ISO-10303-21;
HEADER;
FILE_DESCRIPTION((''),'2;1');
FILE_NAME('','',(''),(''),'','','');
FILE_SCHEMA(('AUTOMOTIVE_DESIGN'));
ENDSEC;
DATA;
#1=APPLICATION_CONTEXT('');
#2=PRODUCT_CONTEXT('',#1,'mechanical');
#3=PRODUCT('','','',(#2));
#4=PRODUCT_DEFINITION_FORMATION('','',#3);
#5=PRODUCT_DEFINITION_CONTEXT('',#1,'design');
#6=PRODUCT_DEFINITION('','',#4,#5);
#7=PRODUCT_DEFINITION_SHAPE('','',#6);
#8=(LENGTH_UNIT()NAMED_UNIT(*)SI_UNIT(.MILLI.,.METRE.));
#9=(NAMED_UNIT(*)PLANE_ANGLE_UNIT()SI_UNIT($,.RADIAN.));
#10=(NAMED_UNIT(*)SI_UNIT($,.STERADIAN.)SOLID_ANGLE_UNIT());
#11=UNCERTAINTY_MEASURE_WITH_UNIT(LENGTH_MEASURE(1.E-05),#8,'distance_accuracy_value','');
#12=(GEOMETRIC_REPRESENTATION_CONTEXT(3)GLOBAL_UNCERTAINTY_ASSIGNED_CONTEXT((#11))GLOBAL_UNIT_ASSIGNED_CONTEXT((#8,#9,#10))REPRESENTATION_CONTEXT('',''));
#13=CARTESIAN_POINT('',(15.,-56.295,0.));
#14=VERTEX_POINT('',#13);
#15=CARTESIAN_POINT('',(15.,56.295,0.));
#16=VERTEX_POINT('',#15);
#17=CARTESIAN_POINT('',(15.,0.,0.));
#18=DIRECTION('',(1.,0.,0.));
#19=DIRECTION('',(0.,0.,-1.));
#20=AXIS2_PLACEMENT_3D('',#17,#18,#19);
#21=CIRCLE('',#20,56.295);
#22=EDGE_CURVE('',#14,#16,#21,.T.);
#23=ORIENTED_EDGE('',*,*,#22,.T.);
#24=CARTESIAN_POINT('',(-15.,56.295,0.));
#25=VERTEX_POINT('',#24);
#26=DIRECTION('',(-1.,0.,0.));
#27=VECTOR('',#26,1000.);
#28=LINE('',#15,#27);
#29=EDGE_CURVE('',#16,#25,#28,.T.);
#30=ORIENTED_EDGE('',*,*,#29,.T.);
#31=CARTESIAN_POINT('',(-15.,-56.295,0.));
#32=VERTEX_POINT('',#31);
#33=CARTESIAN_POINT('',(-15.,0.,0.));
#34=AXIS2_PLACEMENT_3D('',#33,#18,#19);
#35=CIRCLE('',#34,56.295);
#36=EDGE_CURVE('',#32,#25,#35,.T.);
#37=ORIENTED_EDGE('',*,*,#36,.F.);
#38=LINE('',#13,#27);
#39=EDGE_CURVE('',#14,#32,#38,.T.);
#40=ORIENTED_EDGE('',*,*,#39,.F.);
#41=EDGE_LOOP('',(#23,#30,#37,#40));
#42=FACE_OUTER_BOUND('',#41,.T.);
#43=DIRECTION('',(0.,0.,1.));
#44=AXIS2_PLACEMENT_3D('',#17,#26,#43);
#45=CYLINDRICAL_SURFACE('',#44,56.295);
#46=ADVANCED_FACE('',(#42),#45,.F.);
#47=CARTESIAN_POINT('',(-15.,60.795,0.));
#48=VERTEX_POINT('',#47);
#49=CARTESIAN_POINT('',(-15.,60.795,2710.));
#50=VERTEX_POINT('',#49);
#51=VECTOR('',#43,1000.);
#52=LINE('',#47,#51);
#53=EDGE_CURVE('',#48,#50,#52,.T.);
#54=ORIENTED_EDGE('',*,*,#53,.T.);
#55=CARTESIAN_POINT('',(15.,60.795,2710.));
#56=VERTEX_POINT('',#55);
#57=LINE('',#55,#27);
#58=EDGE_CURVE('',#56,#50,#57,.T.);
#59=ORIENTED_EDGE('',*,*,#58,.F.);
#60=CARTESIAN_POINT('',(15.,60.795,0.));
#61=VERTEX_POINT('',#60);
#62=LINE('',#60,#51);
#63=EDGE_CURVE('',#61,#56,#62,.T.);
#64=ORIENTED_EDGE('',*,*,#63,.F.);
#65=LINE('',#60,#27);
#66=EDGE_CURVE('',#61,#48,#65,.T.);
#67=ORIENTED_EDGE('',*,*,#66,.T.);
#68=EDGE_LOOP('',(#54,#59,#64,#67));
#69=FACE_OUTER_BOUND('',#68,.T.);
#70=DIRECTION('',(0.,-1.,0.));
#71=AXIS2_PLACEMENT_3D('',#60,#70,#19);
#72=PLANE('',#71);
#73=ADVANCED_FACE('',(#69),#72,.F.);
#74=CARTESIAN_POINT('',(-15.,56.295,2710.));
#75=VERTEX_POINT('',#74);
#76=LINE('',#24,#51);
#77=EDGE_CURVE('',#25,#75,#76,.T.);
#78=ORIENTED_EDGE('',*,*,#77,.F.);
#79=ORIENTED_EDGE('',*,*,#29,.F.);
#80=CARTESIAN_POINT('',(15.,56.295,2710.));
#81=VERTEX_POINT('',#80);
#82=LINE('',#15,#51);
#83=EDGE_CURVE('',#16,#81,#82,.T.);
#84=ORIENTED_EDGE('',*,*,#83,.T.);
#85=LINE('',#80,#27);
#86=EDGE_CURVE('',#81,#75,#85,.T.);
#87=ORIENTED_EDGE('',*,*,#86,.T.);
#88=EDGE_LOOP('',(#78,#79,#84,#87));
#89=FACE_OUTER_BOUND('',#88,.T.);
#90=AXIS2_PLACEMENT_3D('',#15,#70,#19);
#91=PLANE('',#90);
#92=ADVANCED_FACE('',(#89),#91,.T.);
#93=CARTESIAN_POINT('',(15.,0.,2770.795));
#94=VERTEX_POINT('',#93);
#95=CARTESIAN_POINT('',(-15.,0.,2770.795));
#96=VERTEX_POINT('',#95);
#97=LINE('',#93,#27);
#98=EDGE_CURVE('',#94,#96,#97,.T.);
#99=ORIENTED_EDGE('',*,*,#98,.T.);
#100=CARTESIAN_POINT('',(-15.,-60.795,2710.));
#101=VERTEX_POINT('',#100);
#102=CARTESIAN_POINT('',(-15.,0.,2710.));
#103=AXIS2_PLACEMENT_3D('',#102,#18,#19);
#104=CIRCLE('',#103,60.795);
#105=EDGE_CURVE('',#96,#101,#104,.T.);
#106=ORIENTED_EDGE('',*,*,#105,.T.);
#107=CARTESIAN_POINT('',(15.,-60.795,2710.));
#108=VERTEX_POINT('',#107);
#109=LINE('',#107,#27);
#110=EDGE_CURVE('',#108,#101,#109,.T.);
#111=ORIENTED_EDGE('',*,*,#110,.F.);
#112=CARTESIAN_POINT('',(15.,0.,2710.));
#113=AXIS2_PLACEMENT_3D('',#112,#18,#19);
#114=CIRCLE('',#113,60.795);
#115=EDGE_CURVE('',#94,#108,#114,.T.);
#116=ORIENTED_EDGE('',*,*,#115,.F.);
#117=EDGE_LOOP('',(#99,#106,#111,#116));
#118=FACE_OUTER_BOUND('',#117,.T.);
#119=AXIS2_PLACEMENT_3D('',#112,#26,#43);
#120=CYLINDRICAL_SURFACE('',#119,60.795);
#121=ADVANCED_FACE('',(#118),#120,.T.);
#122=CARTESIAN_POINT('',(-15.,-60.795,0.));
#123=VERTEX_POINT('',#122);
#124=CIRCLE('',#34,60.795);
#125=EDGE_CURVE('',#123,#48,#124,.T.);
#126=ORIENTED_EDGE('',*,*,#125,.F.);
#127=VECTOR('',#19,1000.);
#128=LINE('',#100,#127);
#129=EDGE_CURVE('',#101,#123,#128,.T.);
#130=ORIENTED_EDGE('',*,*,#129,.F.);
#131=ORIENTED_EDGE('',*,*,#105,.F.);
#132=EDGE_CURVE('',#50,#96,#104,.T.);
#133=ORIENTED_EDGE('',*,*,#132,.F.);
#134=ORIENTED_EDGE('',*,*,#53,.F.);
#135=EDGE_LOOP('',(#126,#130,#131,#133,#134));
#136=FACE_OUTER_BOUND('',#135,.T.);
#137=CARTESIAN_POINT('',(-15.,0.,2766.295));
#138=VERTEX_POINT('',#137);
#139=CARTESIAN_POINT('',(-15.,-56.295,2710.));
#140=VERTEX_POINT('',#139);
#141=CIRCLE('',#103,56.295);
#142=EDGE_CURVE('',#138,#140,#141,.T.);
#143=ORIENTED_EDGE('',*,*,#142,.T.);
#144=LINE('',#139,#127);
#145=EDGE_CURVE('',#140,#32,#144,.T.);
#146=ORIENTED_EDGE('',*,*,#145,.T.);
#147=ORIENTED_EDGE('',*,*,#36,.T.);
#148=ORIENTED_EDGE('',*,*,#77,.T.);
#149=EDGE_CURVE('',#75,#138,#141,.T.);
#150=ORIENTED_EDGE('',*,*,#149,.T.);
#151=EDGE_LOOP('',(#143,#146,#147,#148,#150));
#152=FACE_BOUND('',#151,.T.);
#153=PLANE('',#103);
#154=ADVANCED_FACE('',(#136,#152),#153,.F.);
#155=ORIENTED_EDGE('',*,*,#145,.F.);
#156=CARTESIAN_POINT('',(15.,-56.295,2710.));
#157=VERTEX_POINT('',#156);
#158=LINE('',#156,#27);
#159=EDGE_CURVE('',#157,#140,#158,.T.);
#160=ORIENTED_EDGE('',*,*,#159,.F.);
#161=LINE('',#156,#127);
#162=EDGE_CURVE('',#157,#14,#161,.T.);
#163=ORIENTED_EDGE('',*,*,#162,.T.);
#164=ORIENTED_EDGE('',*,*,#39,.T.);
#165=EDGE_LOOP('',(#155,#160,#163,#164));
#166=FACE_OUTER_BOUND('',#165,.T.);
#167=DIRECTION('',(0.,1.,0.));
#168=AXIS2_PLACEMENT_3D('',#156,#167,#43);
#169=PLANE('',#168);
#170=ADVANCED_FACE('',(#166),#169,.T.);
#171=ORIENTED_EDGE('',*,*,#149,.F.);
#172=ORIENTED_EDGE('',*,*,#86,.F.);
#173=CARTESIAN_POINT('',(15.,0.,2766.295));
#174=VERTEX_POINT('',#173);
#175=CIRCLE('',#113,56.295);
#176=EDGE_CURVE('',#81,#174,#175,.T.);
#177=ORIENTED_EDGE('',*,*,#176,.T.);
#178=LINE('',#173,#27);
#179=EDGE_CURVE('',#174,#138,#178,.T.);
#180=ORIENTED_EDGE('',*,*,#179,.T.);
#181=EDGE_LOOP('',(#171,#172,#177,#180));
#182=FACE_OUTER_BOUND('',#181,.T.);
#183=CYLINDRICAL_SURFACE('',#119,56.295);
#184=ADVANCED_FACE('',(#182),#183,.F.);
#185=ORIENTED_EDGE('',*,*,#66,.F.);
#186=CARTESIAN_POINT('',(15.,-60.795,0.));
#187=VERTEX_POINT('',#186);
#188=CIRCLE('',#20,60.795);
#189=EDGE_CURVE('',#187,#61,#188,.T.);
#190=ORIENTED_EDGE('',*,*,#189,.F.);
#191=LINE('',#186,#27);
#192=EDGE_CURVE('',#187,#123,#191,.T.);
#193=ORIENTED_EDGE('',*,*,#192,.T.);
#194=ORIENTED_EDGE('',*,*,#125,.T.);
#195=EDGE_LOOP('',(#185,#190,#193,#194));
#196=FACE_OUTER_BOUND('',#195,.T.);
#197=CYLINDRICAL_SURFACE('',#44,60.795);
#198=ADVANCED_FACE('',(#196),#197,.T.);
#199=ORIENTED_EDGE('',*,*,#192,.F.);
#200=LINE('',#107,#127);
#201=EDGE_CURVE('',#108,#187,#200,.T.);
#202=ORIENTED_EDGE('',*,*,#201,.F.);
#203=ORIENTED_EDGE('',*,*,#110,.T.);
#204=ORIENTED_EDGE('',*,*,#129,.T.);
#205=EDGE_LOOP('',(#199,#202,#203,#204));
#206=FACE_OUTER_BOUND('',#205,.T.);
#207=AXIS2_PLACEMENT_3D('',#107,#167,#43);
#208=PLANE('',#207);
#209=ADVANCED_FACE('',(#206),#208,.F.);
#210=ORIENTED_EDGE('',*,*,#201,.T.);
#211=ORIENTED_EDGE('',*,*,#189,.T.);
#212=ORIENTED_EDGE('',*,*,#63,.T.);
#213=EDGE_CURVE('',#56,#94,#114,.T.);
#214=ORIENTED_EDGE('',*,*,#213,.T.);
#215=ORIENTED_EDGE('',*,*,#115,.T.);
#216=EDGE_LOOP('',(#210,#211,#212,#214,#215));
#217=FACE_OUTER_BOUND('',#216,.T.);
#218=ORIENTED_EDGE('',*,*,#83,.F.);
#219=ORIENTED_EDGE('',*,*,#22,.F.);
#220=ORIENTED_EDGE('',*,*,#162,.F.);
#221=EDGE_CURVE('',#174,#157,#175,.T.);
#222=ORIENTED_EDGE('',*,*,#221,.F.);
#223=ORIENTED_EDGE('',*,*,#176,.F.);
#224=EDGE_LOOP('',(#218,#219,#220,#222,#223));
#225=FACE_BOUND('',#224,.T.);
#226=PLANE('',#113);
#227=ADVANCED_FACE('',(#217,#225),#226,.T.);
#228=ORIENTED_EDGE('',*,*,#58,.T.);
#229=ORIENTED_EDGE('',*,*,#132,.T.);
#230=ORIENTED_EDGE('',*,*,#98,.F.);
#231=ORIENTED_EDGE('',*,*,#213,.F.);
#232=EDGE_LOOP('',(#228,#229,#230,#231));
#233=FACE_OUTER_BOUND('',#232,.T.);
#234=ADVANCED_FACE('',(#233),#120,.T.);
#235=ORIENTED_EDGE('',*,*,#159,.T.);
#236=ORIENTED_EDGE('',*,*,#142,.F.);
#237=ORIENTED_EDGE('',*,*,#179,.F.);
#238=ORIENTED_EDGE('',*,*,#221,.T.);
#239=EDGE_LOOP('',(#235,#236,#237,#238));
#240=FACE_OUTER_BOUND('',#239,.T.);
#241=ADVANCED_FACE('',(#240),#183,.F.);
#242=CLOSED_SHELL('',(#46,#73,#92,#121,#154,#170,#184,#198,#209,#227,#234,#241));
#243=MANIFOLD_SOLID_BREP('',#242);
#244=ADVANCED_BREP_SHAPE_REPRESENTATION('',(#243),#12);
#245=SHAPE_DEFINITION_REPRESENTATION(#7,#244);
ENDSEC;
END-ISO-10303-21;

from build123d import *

# Parameters (mm, degrees)
EXTRUDE_1_DEPTH = 15


with BuildPart() as part:
    # 草图2 → 拉伸-薄壁1 (new, symmetric)
    with BuildSketch(Plane(origin=(0, 0, 0), x_dir=(0, 0, -1), z_dir=(1, 0, 0))):
        with BuildLine():
            Line((-2710, -60.795), (0, -60.795))
            ThreePointArc((0, -60.795), (60.795, 0), (0, 60.795))
            Line((0, 60.795), (-2710, 60.795))
            ThreePointArc((-2710, 60.795), (-2770.795, 0), (-2710, -60.795))
        make_face()
        with BuildLine():
            Line((-2710, -56.295), (0, -56.295))
            ThreePointArc((0, -56.295), (56.295, 0), (0, 56.295))
            Line((0, 56.295), (-2710, 56.295))
            ThreePointArc((-2710, 56.295), (-2766.295, 0), (-2710, -56.295))
        make_face(mode=Mode.SUBTRACT)
    extrude(amount=EXTRUDE_1_DEPTH, both=True)


solid = part.part
